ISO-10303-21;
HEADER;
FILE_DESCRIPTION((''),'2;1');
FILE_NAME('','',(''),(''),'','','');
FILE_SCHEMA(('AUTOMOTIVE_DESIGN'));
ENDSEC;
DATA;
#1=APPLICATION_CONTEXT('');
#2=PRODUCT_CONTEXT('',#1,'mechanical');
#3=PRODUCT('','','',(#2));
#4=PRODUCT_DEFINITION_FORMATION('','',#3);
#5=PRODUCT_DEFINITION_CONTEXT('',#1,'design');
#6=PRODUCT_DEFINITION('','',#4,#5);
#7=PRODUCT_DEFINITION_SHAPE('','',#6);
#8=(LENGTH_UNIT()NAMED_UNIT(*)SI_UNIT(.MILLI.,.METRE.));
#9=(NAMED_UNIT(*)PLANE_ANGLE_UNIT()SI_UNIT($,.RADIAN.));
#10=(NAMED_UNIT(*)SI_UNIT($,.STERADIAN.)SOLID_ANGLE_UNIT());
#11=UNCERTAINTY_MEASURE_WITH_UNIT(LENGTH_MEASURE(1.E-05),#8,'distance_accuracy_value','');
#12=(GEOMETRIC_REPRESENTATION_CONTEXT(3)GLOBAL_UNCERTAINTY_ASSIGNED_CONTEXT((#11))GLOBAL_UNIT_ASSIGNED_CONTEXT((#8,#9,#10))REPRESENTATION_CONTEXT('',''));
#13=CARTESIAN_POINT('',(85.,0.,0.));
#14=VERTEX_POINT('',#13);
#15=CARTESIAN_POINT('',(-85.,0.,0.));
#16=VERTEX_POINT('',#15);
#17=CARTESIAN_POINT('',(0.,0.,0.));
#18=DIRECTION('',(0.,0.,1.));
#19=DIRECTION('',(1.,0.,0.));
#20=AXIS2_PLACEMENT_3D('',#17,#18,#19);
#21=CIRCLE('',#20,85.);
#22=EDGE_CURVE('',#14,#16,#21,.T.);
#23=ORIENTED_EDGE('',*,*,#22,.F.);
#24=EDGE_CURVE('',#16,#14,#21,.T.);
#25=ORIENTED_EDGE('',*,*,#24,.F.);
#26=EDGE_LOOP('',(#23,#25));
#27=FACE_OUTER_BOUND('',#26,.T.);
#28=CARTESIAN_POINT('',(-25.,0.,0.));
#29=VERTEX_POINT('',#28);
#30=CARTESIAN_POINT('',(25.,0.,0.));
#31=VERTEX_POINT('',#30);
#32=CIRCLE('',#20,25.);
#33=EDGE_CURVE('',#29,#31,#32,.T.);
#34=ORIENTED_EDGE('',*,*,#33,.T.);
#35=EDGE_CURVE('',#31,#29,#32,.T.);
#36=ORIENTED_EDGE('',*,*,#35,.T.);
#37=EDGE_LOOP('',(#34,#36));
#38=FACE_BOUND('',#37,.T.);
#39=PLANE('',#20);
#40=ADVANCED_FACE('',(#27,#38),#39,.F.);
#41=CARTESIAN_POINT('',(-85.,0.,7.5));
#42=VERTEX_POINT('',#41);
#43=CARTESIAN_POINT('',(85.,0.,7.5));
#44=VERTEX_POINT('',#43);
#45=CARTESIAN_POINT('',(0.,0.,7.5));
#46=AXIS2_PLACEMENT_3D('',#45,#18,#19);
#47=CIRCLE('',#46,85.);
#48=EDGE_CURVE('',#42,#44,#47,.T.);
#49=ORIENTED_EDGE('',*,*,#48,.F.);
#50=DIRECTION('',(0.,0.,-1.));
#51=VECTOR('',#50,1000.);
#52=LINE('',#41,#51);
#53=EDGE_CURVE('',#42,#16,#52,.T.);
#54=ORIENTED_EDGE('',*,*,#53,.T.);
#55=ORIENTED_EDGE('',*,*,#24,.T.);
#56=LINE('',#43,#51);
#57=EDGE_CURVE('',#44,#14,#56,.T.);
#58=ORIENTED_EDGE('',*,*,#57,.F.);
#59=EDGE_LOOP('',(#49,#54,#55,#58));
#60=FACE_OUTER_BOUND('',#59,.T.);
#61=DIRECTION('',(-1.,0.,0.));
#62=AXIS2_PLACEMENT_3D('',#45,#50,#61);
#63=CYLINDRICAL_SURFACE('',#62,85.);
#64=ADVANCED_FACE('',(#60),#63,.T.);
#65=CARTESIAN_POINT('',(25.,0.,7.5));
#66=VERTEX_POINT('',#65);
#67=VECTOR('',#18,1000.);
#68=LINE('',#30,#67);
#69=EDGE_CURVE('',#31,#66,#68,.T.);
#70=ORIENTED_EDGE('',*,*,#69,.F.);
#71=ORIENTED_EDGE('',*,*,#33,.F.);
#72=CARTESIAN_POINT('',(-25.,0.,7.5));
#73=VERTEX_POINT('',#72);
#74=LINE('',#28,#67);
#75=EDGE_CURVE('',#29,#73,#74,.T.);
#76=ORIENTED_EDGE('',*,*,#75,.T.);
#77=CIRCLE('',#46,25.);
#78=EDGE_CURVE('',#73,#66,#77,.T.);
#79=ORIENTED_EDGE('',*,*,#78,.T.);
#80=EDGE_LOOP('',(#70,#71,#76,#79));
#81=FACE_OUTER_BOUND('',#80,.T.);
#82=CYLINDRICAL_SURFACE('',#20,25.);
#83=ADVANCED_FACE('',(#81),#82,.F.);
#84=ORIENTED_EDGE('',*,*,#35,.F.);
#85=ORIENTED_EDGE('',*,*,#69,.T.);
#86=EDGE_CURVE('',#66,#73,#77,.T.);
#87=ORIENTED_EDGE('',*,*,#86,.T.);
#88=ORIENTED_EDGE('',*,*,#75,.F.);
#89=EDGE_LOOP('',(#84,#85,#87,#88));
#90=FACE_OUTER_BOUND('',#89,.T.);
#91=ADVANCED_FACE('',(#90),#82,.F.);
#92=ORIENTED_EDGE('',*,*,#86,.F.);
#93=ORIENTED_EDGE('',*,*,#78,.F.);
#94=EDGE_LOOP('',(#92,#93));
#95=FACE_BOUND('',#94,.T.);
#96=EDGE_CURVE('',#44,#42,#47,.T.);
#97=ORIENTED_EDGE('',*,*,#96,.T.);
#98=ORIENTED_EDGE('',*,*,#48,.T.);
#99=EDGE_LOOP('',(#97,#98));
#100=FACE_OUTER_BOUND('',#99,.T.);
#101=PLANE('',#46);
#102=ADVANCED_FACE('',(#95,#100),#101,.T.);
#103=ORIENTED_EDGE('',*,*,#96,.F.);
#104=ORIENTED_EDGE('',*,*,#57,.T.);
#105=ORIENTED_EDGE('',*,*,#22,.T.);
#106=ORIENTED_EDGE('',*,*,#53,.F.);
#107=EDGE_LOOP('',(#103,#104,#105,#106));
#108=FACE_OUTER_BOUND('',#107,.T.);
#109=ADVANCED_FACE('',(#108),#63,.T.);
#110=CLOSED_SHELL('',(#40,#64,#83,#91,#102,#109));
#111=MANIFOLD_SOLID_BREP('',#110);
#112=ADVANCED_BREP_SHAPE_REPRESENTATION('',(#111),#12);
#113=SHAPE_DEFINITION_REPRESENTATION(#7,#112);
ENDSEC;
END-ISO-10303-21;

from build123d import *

# Parameters (mm, degrees)
SKETCH1_R               = 85
BOSS_EXTRUDE1_DEPTH     = 7.5
CUT_EXTRUDE1_DEPTH      = 121.441894704
CUT_EXTRUDE1_DEPTH_BACK = 121.441894704
SKETCH2_R               = 25


with BuildPart() as part:
    # Sketch1 → Boss-Extrude1 (new body)
    with BuildSketch(Plane.XY):
        Circle(SKETCH1_R)
    extrude(amount=BOSS_EXTRUDE1_DEPTH)

    # Sketch2 → Cut-Extrude1 (cut, two sides: drawn at the far end of the back side and taken through both)
    with BuildSketch(Plane.XY.offset(7.5).offset(-CUT_EXTRUDE1_DEPTH_BACK)):
        Circle(SKETCH2_R)
    extrude(amount=CUT_EXTRUDE1_DEPTH + CUT_EXTRUDE1_DEPTH_BACK, mode=Mode.SUBTRACT)


solid = part.part
